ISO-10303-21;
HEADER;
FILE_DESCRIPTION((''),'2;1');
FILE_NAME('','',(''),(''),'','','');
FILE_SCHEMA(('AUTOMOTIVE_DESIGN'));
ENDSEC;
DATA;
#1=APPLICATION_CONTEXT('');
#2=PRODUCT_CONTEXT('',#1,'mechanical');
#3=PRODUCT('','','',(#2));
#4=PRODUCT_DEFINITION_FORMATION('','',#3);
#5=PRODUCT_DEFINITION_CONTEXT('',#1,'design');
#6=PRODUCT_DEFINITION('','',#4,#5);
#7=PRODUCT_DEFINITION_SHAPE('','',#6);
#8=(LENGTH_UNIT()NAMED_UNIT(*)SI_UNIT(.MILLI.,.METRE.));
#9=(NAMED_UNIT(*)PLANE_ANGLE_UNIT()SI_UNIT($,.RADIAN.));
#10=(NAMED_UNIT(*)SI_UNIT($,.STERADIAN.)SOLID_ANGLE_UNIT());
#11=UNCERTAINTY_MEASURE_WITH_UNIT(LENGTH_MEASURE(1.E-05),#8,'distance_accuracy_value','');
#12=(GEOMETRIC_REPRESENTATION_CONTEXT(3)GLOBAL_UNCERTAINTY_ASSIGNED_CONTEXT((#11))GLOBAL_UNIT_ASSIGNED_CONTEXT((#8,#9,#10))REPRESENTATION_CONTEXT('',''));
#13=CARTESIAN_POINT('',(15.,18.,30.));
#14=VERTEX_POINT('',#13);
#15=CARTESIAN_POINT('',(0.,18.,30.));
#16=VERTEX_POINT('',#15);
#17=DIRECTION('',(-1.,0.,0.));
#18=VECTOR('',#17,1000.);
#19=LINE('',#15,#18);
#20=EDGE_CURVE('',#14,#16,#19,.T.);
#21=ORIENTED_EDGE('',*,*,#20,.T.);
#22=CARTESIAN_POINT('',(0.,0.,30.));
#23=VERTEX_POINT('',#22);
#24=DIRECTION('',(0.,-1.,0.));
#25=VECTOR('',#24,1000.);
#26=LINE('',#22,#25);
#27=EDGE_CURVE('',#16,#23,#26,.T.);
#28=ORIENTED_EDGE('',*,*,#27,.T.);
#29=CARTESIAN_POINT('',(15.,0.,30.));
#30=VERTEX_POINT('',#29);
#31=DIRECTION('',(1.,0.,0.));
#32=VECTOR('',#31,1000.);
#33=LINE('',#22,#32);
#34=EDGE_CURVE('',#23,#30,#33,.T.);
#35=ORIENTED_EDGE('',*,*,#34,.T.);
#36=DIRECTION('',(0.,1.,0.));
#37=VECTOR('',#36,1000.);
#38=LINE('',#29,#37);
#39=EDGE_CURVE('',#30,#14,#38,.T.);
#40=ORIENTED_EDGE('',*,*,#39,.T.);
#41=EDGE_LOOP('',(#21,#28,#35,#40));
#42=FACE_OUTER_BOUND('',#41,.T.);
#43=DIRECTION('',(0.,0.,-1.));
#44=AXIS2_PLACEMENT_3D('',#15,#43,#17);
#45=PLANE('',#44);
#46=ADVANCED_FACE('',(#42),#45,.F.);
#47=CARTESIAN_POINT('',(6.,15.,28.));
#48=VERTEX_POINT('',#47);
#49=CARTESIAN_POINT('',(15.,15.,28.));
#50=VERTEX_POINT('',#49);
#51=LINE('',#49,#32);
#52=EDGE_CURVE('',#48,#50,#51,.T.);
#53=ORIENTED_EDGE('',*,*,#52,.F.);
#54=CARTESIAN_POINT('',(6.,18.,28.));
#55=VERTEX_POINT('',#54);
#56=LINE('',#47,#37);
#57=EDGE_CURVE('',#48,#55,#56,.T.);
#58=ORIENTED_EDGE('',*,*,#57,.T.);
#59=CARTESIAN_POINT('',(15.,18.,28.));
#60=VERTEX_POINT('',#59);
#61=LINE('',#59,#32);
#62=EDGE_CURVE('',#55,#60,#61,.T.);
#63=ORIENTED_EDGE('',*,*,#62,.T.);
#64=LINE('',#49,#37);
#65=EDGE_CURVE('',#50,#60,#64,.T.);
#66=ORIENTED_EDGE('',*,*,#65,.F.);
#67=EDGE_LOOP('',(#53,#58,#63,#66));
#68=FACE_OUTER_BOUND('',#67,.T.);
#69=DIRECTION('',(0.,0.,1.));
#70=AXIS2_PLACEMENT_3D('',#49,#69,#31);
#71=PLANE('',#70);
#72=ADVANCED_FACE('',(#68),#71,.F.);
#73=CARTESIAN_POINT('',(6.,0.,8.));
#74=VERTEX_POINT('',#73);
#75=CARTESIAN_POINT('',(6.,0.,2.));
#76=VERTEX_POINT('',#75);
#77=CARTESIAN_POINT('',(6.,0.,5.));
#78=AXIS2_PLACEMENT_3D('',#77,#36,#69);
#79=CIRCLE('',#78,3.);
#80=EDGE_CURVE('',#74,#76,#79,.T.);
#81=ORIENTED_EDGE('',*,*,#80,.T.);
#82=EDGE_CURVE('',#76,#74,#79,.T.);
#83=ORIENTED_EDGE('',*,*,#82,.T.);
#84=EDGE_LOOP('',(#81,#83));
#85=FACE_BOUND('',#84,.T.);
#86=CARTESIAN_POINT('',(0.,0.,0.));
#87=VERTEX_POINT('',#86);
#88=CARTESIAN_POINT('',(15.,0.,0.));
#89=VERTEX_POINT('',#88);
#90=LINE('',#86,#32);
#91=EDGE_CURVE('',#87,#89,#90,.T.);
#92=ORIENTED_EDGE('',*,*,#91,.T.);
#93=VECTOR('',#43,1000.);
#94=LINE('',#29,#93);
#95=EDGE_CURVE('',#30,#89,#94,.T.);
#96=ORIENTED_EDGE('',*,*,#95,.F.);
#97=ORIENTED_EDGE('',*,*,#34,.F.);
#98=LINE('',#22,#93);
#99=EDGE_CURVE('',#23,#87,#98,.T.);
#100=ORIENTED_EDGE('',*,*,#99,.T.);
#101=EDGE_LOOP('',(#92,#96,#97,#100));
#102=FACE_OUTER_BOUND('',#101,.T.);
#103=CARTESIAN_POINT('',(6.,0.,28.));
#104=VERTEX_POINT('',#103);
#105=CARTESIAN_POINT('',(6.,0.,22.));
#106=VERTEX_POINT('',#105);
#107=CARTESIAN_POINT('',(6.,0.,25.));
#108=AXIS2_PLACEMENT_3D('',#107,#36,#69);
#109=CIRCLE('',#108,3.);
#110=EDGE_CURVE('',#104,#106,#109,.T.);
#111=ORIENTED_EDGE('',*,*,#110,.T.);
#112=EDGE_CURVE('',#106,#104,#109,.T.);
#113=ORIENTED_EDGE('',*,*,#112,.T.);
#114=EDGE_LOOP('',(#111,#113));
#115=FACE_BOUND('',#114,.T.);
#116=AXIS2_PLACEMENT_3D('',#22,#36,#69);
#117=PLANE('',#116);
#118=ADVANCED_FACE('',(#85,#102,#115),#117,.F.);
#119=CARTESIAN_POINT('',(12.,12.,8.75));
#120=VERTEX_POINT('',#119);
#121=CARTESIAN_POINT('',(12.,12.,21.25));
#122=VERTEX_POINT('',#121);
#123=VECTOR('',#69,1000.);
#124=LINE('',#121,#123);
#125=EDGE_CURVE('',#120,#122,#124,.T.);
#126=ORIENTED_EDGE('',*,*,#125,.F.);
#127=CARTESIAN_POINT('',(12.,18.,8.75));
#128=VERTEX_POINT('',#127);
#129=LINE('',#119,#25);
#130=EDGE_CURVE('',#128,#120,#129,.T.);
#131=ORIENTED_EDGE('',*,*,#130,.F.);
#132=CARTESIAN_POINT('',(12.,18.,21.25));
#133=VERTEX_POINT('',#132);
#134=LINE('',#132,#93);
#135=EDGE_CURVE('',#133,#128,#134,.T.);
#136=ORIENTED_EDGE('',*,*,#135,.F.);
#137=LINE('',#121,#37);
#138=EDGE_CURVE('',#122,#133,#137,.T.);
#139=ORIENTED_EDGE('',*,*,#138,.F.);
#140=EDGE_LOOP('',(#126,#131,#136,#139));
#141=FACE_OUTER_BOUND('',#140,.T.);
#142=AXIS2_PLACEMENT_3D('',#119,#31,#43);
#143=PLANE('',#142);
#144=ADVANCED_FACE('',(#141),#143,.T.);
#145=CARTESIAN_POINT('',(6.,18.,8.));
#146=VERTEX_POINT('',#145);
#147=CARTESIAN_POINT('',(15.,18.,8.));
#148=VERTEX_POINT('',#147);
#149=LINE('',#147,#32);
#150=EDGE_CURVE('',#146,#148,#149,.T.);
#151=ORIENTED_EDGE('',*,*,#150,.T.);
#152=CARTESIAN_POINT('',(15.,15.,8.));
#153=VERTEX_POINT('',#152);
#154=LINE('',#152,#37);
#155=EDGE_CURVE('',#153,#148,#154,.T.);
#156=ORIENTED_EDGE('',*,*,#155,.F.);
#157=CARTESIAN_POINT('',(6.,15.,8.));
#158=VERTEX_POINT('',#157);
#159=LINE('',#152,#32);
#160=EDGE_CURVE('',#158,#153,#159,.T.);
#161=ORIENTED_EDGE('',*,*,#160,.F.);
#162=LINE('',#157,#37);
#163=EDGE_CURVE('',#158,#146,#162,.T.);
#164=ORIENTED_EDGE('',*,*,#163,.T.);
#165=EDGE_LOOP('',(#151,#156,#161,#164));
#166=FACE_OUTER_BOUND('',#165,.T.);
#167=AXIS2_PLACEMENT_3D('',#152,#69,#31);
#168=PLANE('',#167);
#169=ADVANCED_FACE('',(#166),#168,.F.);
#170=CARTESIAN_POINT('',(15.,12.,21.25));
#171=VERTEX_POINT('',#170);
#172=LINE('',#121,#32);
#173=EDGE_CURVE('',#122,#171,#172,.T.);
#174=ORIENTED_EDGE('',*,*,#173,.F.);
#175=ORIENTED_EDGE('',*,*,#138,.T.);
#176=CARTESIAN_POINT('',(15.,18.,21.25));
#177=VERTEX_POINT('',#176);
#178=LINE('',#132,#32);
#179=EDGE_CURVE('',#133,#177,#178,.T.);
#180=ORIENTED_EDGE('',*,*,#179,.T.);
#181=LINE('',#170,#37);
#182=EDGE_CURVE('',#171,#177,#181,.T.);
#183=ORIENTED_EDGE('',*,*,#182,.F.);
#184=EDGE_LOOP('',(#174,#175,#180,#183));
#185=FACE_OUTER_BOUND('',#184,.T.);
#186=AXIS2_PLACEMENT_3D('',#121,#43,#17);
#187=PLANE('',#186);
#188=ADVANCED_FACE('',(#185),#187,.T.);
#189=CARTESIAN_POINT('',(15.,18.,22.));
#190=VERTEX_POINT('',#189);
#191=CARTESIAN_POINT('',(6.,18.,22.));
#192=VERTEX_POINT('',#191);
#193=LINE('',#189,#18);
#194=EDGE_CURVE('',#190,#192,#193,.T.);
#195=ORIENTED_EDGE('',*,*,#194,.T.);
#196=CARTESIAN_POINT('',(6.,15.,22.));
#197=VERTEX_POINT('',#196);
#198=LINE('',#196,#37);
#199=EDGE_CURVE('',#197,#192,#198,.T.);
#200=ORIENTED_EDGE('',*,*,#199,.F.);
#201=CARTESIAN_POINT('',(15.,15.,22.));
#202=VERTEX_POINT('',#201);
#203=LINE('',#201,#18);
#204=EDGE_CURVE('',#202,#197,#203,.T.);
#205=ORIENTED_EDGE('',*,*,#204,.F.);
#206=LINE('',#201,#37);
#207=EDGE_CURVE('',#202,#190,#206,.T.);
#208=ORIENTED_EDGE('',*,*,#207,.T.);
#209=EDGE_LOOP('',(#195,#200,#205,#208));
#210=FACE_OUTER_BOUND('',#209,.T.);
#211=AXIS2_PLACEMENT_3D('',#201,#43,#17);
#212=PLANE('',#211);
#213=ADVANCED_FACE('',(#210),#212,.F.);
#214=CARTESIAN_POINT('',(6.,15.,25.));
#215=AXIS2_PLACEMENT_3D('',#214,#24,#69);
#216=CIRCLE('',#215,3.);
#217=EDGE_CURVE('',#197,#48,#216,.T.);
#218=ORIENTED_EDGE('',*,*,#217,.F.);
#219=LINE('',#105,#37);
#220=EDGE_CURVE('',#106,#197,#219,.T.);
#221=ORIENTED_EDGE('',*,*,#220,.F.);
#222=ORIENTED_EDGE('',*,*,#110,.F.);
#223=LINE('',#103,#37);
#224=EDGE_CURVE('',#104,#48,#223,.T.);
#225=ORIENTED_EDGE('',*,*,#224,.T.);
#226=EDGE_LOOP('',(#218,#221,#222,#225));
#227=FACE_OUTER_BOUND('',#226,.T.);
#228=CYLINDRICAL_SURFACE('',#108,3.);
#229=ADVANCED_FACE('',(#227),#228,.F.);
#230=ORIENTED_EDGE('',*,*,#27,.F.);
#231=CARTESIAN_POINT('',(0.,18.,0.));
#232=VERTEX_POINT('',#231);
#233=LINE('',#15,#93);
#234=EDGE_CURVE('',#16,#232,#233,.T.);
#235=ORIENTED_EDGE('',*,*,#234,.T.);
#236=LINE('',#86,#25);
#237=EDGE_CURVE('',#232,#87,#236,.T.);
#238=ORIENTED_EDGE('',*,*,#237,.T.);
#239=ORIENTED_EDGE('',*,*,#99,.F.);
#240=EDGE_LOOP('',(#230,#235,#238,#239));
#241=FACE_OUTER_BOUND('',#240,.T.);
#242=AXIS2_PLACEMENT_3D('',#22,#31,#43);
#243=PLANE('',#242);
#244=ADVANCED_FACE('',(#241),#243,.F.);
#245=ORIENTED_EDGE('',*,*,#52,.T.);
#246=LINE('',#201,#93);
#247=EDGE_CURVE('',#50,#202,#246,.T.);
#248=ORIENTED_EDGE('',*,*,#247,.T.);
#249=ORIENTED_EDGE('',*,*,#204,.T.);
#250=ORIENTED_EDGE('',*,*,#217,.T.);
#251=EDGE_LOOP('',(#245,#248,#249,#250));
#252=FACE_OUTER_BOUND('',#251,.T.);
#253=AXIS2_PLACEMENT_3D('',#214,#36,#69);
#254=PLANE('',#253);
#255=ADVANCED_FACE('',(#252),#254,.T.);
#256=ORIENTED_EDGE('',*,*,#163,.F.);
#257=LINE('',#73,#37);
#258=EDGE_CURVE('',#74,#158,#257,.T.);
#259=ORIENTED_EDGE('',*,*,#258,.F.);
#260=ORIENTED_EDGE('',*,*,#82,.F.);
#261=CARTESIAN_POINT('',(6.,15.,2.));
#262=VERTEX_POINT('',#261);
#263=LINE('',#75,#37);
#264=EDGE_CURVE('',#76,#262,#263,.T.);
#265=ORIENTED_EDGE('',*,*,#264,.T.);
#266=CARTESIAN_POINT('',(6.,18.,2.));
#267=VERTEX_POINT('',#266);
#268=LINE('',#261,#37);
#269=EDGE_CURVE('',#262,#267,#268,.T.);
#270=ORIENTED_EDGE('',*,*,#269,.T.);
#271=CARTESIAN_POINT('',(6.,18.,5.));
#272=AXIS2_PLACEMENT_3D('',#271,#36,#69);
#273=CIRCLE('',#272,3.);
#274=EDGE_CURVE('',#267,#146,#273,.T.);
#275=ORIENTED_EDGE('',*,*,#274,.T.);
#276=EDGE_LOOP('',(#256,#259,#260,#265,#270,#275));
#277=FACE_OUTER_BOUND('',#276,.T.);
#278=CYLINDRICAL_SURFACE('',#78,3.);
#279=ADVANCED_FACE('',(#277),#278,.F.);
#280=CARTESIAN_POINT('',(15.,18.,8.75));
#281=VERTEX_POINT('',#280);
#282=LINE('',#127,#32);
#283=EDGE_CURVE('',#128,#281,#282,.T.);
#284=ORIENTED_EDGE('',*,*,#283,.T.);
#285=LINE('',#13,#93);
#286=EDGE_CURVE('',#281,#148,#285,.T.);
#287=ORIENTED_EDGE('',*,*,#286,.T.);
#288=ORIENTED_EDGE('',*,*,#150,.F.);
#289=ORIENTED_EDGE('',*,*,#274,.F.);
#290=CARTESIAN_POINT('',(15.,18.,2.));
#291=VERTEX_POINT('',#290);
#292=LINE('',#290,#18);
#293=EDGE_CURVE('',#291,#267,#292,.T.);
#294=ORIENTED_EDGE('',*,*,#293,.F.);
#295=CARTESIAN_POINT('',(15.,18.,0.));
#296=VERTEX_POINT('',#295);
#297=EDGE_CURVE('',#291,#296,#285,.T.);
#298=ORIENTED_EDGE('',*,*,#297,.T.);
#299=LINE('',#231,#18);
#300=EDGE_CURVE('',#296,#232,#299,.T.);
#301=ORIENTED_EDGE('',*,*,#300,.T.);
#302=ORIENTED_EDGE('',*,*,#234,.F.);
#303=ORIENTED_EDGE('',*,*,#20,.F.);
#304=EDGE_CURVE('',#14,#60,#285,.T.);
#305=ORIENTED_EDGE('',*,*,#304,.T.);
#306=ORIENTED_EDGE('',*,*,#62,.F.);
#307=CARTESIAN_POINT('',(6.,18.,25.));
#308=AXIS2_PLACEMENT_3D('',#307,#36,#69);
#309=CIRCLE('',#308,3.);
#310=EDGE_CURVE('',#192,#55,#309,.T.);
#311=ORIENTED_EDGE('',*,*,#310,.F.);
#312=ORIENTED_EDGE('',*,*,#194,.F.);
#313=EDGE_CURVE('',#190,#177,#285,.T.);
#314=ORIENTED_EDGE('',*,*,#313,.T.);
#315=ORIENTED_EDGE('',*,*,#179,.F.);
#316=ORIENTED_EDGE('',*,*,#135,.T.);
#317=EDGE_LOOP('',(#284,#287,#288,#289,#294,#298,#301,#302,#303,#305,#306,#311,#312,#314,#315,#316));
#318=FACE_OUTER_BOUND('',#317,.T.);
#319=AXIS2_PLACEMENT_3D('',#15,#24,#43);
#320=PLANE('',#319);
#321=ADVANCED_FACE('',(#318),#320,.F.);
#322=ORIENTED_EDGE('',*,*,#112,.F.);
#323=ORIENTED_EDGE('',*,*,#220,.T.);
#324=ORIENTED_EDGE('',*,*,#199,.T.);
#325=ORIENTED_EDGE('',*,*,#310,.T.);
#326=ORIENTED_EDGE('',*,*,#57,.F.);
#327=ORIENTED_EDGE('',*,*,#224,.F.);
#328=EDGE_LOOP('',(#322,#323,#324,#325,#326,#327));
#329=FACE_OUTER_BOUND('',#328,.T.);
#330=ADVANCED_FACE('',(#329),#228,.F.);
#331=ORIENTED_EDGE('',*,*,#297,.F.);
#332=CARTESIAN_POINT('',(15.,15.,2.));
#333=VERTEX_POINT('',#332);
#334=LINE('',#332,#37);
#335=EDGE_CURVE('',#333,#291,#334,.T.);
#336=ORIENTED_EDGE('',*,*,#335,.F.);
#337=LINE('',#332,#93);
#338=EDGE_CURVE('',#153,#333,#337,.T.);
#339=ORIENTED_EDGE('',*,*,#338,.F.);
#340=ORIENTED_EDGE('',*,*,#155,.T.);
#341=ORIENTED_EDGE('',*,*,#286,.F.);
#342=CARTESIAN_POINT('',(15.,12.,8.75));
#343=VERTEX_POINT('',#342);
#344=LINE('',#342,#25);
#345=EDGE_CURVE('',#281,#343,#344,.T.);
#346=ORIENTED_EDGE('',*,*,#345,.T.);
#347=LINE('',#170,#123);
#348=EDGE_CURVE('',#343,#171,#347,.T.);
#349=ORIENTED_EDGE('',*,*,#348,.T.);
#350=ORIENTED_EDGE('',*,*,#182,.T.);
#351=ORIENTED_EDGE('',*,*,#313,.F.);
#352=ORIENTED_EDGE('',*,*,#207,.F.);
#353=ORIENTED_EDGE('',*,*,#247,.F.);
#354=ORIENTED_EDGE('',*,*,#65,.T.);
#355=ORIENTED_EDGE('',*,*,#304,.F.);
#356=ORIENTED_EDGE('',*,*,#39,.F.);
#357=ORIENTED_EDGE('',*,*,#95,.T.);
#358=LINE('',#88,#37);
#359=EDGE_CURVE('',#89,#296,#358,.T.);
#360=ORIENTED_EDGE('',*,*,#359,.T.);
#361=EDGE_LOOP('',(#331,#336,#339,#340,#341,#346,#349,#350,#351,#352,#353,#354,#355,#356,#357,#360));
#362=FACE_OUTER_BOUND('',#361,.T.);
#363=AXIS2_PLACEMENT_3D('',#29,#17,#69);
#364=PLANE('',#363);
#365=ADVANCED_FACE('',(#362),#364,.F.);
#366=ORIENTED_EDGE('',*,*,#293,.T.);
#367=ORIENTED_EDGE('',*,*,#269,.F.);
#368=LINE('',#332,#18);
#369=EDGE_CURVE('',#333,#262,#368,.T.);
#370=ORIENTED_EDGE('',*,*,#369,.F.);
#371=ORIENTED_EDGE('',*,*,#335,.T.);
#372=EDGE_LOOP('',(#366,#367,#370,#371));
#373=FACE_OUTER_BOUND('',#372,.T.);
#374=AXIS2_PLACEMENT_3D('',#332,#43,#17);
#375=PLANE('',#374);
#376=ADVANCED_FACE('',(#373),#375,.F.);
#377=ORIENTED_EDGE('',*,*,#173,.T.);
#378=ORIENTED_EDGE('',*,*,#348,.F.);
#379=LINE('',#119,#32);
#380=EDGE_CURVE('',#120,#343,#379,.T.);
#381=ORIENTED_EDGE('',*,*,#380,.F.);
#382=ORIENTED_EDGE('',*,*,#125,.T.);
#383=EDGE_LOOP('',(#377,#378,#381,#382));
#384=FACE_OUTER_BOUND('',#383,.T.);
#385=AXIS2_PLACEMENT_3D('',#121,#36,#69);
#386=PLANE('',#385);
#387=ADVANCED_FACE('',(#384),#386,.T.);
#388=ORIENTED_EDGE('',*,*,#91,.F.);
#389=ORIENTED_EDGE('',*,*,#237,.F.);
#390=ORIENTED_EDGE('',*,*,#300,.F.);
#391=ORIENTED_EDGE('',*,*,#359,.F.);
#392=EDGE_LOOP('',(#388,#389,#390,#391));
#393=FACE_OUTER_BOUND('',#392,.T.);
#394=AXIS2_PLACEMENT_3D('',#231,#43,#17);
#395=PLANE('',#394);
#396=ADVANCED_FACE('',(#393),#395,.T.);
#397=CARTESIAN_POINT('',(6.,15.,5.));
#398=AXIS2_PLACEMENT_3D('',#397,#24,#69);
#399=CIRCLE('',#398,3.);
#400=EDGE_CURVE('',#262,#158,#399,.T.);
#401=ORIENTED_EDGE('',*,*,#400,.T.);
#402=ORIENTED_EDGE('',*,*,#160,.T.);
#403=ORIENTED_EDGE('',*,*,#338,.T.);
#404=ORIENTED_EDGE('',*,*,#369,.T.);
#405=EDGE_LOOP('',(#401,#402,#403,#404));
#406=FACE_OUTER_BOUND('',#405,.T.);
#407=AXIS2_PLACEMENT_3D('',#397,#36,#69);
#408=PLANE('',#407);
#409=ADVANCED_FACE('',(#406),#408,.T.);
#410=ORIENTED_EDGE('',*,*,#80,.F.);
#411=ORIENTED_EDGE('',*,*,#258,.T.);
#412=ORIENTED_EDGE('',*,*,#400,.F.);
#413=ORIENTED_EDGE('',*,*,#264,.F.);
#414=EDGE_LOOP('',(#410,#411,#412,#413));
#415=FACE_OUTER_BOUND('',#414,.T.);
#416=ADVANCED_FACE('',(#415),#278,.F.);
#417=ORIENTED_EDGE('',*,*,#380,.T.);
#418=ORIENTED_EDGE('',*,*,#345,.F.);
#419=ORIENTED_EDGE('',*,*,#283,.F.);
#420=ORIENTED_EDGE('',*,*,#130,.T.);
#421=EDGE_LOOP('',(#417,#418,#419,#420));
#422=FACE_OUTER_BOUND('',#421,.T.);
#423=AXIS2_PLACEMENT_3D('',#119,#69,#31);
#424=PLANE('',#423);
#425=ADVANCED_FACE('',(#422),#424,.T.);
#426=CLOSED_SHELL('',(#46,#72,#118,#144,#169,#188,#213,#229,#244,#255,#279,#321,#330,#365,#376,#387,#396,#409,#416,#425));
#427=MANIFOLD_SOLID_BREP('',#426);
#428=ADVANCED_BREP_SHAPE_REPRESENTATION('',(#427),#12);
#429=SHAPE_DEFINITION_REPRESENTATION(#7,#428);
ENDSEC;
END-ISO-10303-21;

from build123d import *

# Parameters (mm, degrees)
SKETCH_1_W             = 15
SKETCH_1_H             = 18
EXTRUDE_1_DEPTH        = 30
SKETCH_2_R             = 3
CUT_EXTRUDE_1_DEPTH    = 39.065732621
CUT_EXTRUDE_3_DEPTH    = 3
PATTERN_LINEAR_1_COUNT = 2
PATTERN_LINEAR_1_PITCH = 20
SKETCH_5_W             = 6
SKETCH_5_H             = 12.5
CUT_EXTRUDE_4_DEPTH    = 3


with BuildPart() as part:
    # 草图1 → 拉伸1 (new body)
    with BuildSketch(Plane.XY):
        with Locations((7.5, 9)):
            Rectangle(SKETCH_1_W, SKETCH_1_H)
    extrude(amount=EXTRUDE_1_DEPTH)

    # 草图2 → 切除-拉伸1 (cut, through all)
    with BuildSketch(Plane(origin=(0, 18, 0), x_dir=(-1, 0, 0), z_dir=(0, 1, 0))):
        with Locations(Location((-6, 5, 0), (0, 0, 90))):
            Circle(SKETCH_2_R)
    cut_extrude_1 = extrude(amount=-CUT_EXTRUDE_1_DEPTH, mode=Mode.SUBTRACT)

    # 草图4 → 切除-拉伸3 (cut)
    with BuildSketch(Plane(origin=(0, 18, 0), x_dir=(-1, 0, 0), z_dir=(0, 1, 0))):
        with BuildLine():
            Line((-15, 2), (-6, 2))
            ThreePointArc((-6, 2), (-3, 5), (-6, 8))
            Line((-6, 8), (-15, 8))
            Line((-15, 8), (-15, 2))
        make_face()
    cut_extrude_3 = extrude(amount=-CUT_EXTRUDE_3_DEPTH, mode=Mode.SUBTRACT)

    # 阵列(线性)1: 切除-拉伸1, 切除-拉伸3 ×2
    with Locations(*[(0, 0, i * PATTERN_LINEAR_1_PITCH) for i in range(1, PATTERN_LINEAR_1_COUNT)]):
        add(cut_extrude_1, mode=Mode.SUBTRACT)
        add(cut_extrude_3, mode=Mode.SUBTRACT)

    # 草图5 → 切除-拉伸4 (cut)
    with BuildSketch(Plane(origin=(15, 3, 0), x_dir=(0, 1, 0), z_dir=(-1, 0, 0))):
        with Locations((12, -15)):
            Rectangle(SKETCH_5_W, SKETCH_5_H)
    extrude(amount=CUT_EXTRUDE_4_DEPTH, mode=Mode.SUBTRACT)


solid = part.part
